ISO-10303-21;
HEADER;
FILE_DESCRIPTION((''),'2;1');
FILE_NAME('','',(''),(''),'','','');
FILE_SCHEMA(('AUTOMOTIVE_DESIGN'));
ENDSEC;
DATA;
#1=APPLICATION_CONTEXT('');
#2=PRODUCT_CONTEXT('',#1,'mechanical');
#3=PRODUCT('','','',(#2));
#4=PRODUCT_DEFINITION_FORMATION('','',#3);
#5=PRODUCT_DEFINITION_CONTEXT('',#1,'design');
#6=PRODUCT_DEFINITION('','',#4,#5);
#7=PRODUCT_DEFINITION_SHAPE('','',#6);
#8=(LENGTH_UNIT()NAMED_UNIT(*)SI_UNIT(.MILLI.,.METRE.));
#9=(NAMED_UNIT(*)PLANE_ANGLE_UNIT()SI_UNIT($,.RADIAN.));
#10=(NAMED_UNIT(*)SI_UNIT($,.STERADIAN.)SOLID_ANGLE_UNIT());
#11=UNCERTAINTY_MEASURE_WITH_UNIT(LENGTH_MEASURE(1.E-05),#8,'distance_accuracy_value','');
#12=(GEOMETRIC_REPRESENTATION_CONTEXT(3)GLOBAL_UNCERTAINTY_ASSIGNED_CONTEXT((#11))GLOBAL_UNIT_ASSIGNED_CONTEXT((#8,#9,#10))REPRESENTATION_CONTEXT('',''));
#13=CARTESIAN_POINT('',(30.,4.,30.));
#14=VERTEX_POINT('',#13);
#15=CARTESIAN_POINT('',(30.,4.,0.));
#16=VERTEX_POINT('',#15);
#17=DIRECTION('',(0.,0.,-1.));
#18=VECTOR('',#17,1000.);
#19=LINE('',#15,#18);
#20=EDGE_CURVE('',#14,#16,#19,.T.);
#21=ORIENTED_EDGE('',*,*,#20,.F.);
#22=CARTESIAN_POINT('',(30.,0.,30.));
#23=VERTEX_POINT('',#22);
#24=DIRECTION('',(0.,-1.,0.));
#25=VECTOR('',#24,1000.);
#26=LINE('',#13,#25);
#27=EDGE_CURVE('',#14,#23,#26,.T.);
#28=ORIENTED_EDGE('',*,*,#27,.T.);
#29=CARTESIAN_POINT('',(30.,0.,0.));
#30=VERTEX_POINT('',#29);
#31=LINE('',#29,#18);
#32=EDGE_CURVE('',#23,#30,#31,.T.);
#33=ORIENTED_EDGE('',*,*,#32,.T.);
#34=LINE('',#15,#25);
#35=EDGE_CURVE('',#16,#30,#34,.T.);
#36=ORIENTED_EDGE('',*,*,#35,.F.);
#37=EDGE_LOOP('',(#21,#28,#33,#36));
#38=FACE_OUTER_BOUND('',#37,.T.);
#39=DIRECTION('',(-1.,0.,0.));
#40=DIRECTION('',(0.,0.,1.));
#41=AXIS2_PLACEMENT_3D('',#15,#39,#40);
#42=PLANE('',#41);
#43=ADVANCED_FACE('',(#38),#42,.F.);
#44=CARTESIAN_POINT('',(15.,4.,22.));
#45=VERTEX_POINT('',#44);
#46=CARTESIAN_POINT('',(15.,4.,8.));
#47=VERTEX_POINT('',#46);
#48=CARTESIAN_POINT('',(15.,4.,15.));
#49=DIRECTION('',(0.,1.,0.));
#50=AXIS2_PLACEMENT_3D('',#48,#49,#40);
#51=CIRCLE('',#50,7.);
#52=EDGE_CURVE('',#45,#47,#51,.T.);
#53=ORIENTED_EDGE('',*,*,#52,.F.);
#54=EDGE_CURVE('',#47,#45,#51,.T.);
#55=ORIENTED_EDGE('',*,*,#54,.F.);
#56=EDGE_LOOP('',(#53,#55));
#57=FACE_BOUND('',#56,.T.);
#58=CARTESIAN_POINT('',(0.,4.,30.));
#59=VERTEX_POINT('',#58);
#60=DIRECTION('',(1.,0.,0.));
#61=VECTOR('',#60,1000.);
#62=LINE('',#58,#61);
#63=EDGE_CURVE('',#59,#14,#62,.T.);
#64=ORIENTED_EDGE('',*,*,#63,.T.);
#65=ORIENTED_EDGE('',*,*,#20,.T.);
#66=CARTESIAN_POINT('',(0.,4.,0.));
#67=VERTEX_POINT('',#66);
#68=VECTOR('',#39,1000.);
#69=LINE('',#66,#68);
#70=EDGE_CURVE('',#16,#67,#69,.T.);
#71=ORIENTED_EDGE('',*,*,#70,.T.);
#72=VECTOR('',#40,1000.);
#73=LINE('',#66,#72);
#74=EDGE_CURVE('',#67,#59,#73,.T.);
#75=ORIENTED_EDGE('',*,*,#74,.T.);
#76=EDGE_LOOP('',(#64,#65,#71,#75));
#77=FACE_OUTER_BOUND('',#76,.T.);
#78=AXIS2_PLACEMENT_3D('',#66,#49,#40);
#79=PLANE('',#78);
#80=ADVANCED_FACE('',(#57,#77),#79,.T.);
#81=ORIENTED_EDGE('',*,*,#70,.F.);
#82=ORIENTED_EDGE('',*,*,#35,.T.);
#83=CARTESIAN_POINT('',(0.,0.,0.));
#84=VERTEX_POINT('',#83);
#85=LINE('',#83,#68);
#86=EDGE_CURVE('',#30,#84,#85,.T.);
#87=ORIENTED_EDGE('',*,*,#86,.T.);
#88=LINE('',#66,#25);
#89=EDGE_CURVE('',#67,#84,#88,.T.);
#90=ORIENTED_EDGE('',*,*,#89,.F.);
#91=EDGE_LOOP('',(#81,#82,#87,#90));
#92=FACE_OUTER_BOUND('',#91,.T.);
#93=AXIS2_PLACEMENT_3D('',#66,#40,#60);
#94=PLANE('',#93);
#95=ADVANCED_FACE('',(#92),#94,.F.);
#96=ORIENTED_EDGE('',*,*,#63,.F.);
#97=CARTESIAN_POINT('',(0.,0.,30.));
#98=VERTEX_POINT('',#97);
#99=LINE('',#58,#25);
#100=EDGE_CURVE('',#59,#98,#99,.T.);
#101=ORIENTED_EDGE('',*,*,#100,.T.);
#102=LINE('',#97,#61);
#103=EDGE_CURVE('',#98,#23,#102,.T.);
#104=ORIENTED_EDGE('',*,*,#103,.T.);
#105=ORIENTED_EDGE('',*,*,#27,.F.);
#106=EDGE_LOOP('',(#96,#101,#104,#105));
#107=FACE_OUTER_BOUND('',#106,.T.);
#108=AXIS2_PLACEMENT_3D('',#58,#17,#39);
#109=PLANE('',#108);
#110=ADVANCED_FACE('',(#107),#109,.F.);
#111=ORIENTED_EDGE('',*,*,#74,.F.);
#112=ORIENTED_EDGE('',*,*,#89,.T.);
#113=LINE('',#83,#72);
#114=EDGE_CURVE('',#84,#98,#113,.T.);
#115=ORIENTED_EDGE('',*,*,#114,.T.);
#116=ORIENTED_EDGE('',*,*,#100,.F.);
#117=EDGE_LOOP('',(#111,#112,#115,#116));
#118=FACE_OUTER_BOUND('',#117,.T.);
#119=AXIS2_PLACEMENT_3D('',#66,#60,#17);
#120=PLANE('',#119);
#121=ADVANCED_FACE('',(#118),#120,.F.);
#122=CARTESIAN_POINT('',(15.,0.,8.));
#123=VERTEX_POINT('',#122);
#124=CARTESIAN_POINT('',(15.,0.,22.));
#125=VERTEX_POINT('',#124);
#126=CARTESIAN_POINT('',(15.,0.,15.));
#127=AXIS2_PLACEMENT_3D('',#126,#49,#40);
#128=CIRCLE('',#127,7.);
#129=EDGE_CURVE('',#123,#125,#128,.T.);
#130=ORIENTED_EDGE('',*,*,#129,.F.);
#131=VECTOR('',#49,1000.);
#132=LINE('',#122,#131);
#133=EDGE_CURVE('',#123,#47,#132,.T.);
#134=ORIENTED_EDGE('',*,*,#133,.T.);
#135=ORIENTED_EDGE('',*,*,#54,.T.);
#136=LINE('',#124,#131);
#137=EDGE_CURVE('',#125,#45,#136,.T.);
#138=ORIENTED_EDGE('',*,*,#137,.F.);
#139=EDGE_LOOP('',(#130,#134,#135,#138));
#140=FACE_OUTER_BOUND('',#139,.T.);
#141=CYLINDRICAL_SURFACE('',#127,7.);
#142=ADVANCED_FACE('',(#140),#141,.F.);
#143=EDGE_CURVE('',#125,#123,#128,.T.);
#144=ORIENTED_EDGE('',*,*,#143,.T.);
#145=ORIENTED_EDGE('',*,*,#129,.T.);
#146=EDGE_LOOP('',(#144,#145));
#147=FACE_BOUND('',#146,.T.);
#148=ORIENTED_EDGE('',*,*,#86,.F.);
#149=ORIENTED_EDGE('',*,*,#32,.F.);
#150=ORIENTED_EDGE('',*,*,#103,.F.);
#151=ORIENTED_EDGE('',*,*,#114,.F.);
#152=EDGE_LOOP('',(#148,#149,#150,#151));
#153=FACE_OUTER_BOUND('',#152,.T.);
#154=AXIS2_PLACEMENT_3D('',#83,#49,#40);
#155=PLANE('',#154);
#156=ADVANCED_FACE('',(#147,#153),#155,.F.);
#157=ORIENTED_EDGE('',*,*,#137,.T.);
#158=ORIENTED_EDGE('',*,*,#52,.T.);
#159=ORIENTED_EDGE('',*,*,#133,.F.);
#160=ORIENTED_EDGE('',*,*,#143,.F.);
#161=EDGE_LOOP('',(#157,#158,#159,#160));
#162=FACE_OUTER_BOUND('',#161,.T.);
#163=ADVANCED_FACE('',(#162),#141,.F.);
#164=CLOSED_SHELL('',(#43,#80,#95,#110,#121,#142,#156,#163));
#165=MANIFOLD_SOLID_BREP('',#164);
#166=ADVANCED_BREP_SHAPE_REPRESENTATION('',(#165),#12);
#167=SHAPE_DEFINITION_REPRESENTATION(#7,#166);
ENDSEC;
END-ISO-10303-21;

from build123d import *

# Parameters (mm, degrees)
SKETCH1_W           = 30
SKETCH1_H           = 30
BOSS_EXTRUDE1_DEPTH = 4
SKETCH3_R           = 7
CUT_EXTRUDE2_DEPTH  = 43.614551505


with BuildPart() as part:
    # Sketch1 → Boss-Extrude1 (new body)
    with BuildSketch(Plane(origin=(0, 0, 0), x_dir=(1, 0, 0), z_dir=(0, 1, 0))):
        with Locations((15, -15)):
            Rectangle(SKETCH1_W, SKETCH1_H)
    extrude(amount=BOSS_EXTRUDE1_DEPTH)

    # Sketch3 → Cut-Extrude2 (cut, through all)
    with BuildSketch(Plane(origin=(0, 4, 0), x_dir=(1, 0, 0), z_dir=(0, 1, 0))):
        with Locations(Location((15, -15, 0), (0, 0, 270))):
            Circle(SKETCH3_R)
    extrude(amount=-CUT_EXTRUDE2_DEPTH, mode=Mode.SUBTRACT)


solid = part.part
